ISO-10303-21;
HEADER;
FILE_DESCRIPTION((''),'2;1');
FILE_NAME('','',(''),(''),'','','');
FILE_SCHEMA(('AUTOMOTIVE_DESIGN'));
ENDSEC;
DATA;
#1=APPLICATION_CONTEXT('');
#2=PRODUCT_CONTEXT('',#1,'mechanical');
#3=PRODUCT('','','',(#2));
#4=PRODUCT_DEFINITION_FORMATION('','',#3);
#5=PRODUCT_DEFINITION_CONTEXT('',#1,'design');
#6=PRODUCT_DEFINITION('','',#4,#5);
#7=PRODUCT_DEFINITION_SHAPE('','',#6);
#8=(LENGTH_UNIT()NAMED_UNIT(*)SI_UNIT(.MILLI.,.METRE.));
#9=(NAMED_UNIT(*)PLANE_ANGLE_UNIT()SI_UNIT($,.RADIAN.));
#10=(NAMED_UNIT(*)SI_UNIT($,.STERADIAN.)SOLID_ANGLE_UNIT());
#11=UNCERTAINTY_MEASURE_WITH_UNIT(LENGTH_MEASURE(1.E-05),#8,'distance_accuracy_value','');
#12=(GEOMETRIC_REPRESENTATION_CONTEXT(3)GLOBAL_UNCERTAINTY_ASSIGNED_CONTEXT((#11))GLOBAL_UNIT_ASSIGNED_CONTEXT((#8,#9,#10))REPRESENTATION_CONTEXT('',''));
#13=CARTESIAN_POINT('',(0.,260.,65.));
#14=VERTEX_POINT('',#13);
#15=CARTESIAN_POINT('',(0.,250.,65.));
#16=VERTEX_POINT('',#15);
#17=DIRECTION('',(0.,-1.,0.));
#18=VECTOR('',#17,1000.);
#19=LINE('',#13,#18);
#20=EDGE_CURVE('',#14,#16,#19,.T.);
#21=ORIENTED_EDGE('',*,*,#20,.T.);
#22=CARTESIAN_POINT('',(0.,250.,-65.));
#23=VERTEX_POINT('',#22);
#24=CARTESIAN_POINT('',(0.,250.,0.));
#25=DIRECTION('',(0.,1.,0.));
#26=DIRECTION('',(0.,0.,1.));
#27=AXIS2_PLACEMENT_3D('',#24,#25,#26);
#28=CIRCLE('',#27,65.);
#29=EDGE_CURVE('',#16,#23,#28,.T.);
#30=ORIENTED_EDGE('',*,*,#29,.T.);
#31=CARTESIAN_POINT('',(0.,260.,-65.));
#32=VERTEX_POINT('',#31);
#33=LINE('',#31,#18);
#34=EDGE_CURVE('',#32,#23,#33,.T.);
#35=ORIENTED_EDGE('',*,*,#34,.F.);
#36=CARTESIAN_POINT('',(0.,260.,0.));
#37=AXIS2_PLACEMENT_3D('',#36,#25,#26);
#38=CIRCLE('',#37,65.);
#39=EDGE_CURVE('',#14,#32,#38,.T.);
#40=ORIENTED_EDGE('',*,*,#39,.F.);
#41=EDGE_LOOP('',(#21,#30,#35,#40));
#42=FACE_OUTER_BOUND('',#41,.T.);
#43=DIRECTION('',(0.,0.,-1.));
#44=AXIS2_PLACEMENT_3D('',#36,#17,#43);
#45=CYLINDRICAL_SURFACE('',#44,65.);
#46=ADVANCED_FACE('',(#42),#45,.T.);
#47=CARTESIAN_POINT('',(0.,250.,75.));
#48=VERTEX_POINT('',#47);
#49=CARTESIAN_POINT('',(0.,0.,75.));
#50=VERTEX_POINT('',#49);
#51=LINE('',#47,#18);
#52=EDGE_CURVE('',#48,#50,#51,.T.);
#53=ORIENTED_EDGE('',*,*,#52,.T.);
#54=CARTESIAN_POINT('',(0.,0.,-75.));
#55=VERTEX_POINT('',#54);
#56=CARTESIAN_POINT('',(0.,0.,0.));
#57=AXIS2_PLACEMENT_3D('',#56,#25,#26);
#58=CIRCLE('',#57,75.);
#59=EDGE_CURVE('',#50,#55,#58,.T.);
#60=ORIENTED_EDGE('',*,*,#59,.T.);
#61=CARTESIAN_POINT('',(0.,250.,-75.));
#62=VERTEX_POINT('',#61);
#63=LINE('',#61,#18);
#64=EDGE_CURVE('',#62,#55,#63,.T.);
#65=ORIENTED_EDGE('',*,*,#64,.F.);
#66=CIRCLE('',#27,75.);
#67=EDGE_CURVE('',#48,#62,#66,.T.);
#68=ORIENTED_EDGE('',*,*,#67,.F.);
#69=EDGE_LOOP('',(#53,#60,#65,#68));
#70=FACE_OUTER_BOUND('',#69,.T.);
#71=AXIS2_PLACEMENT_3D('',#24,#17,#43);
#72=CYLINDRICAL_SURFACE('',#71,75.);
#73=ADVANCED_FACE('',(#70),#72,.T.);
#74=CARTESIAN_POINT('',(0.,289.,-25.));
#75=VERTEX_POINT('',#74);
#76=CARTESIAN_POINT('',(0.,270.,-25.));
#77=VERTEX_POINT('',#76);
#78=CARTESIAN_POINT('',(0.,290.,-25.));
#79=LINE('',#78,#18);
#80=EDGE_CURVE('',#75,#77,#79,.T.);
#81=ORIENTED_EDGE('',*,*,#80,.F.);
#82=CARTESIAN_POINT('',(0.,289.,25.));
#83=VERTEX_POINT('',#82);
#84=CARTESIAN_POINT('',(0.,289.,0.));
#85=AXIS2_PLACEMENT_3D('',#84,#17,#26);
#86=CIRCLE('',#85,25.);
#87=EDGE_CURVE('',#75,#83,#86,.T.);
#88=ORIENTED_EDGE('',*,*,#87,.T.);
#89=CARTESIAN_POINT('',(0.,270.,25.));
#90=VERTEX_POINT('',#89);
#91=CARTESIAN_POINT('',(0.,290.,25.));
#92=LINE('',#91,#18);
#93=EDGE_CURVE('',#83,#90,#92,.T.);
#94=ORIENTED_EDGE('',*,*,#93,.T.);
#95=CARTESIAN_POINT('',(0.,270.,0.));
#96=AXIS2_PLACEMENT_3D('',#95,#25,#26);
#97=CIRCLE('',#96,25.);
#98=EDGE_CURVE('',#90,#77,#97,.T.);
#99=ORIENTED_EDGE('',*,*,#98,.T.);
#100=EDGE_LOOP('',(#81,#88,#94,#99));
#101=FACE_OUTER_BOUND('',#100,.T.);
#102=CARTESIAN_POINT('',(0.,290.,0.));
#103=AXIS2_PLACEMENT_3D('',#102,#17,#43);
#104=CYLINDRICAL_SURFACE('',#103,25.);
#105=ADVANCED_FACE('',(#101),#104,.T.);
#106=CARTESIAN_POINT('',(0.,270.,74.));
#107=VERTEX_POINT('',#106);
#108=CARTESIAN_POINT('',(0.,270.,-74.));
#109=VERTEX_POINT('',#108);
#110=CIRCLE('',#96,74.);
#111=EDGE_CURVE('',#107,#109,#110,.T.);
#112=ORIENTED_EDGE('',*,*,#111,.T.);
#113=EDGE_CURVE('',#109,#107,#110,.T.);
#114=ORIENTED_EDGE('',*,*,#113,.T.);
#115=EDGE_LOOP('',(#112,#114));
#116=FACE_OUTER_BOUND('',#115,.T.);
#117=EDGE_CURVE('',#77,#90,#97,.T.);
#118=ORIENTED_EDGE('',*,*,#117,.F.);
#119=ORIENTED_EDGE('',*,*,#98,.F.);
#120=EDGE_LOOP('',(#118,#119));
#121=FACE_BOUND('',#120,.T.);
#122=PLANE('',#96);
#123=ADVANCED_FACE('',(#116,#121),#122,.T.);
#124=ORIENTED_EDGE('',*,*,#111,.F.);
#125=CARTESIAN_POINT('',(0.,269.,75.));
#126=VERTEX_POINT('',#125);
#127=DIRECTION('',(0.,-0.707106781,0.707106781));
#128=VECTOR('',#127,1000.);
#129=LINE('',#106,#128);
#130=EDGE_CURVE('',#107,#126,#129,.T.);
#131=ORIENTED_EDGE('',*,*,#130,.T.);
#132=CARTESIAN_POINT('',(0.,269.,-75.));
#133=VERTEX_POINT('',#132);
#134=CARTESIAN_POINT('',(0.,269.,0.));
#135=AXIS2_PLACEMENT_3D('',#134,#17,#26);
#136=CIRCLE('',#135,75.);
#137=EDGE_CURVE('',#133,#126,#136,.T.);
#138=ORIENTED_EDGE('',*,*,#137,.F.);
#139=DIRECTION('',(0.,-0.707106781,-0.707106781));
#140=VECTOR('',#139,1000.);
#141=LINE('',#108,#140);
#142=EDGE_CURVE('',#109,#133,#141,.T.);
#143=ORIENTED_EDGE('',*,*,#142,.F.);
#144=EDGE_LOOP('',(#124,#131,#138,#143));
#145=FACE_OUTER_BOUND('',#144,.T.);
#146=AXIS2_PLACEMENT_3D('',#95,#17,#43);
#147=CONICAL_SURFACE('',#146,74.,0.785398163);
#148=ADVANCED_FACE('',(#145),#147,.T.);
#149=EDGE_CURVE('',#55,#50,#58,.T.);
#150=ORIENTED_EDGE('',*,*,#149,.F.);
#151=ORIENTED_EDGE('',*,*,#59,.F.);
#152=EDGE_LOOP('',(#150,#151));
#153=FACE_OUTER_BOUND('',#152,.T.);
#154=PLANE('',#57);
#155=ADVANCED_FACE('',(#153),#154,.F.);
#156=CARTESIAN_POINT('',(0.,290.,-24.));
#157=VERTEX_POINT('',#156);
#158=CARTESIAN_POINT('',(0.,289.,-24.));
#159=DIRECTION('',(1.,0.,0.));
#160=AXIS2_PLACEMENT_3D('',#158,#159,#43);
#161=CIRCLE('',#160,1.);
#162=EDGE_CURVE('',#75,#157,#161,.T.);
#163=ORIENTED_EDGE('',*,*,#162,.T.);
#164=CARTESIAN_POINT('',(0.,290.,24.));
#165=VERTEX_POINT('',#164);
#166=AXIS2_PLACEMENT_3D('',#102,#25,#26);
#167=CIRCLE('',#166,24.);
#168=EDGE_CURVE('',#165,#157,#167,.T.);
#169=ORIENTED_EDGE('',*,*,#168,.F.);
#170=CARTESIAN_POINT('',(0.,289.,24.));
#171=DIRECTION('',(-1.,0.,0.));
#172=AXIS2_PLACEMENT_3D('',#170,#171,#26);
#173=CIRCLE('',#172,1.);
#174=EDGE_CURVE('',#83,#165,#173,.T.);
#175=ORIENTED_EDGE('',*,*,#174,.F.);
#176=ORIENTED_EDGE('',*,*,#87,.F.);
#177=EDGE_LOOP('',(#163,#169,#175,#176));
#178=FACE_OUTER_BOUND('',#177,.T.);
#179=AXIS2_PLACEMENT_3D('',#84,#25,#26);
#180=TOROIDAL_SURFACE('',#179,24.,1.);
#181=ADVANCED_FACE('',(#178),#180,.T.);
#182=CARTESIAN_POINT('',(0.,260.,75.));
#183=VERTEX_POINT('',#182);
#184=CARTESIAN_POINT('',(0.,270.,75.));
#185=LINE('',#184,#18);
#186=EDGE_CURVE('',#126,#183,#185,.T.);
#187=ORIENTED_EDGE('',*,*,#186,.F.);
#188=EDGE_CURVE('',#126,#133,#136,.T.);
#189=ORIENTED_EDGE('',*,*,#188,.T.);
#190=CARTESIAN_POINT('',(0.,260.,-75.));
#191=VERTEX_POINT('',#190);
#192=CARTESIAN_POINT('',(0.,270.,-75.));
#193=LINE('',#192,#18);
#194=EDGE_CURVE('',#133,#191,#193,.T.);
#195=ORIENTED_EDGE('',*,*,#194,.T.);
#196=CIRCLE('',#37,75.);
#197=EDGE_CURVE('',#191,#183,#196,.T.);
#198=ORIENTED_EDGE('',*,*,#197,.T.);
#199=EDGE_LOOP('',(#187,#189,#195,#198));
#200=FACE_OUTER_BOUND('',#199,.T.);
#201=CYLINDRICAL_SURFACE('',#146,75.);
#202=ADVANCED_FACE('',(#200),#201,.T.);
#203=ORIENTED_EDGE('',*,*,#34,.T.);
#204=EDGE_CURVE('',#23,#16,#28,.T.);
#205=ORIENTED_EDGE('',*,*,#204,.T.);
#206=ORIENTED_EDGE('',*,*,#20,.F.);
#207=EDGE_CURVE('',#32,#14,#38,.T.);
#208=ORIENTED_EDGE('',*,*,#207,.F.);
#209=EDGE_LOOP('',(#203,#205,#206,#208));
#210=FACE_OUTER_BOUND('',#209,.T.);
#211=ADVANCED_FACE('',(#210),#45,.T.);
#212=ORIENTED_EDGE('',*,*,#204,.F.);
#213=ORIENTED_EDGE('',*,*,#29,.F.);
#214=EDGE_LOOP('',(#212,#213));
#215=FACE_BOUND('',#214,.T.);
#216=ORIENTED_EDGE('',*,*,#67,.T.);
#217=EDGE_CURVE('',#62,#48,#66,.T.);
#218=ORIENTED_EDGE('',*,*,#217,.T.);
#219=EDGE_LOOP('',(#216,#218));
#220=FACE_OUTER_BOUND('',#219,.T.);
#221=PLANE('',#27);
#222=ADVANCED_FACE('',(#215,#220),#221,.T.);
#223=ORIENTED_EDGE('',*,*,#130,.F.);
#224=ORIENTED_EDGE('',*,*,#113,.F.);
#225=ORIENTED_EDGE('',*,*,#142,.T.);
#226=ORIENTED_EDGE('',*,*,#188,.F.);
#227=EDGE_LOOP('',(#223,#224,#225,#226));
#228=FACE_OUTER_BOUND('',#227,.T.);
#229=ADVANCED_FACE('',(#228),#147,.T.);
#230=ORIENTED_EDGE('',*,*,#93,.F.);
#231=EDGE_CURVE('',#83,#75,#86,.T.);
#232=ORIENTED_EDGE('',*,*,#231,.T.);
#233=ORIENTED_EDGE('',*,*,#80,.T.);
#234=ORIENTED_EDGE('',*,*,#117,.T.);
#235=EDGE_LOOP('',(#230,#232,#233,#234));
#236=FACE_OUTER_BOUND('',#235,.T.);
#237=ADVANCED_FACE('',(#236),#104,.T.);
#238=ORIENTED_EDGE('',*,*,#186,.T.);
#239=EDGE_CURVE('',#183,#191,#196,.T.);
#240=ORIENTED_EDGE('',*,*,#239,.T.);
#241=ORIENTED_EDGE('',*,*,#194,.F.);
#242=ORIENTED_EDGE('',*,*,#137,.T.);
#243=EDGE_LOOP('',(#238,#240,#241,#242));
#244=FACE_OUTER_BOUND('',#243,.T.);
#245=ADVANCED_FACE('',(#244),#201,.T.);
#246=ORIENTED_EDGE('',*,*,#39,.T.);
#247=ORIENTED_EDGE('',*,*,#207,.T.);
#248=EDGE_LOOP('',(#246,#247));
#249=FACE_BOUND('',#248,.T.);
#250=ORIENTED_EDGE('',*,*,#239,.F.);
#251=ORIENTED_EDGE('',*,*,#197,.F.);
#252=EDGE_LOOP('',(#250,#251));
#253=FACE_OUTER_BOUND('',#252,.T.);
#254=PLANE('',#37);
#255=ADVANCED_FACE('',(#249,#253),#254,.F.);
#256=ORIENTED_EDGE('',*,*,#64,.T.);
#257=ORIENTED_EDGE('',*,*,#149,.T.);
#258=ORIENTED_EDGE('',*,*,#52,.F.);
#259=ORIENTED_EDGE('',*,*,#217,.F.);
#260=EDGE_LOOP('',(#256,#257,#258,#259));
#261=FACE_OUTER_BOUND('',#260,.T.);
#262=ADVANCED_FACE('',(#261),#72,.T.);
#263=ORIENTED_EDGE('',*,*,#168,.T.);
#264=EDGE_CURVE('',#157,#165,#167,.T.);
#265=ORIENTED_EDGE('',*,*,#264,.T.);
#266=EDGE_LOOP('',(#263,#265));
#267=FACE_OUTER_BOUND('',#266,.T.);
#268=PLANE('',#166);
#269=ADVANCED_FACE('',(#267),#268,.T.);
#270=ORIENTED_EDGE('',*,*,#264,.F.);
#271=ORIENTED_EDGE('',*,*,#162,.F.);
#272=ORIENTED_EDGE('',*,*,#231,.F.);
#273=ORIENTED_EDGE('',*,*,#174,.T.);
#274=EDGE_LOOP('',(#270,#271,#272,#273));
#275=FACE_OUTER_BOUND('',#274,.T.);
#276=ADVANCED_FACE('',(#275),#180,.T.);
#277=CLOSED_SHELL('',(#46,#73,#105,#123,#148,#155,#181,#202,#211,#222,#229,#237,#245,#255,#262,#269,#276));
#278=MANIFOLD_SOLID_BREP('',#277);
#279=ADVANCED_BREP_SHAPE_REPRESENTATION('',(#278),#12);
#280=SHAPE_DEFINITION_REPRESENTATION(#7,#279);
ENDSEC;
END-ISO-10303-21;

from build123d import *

# Parameters (mm, degrees)
SKETCH1_R           = 75
BOSS_EXTRUDE1_DEPTH = 250
SKETCH2_R           = 65
BOSS_EXTRUDE2_DEPTH = 10
SKETCH3_R           = 75
BOSS_EXTRUDE3_DEPTH = 10
SKETCH4_R           = 25
BOSS_EXTRUDE4_DEPTH = 20
FILLET1_R           = 1
CHAMFER1_SIZE       = 1


with BuildPart() as part:
    # Sketch1 → Boss-Extrude1 (new body)
    with BuildSketch(Plane(origin=(0, 0, 0), x_dir=(1, 0, 0), z_dir=(0, 1, 0))):
        with Locations(Location((0, 0, 0), (0, 0, 270))):
            Circle(SKETCH1_R)
    extrude(amount=BOSS_EXTRUDE1_DEPTH)

    # Sketch2 → Boss-Extrude2 (add)
    with BuildSketch(Plane(origin=(0, 250, 0), x_dir=(1, 0, 0), z_dir=(0, 1, 0))):
        with Locations(Location((0, 0, 0), (0, 0, 270))):
            Circle(SKETCH2_R)
    extrude(amount=BOSS_EXTRUDE2_DEPTH)

    # Sketch3 → Boss-Extrude3 (add)
    with BuildSketch(Plane(origin=(0, 260, 0), x_dir=(1, 0, 0), z_dir=(0, 1, 0))):
        with Locations(Location((0, 0, 0), (0, 0, 270))):
            Circle(SKETCH3_R)
    extrude(amount=BOSS_EXTRUDE3_DEPTH)

    # Sketch4 → Boss-Extrude4 (add)
    with BuildSketch(Plane(origin=(0, 270, 0), x_dir=(1, 0, 0), z_dir=(0, 1, 0))):
        with Locations(Location((0, 0, 0), (0, 0, 270))):
            Circle(SKETCH4_R)
    extrude(amount=BOSS_EXTRUDE4_DEPTH)

    # Fillet1
    fillet1_edges = [part.edges().sort_by_distance(p)[0] for p in [
        (0, 290, -25),
    ]]
    fillet(fillet1_edges, radius=FILLET1_R)

    # Chamfer1
    chamfer1_edges = [part.edges().sort_by_distance(p)[0] for p in [
        (0, 270, -75),
    ]]
    chamfer(chamfer1_edges, length=CHAMFER1_SIZE)


solid = part.part
